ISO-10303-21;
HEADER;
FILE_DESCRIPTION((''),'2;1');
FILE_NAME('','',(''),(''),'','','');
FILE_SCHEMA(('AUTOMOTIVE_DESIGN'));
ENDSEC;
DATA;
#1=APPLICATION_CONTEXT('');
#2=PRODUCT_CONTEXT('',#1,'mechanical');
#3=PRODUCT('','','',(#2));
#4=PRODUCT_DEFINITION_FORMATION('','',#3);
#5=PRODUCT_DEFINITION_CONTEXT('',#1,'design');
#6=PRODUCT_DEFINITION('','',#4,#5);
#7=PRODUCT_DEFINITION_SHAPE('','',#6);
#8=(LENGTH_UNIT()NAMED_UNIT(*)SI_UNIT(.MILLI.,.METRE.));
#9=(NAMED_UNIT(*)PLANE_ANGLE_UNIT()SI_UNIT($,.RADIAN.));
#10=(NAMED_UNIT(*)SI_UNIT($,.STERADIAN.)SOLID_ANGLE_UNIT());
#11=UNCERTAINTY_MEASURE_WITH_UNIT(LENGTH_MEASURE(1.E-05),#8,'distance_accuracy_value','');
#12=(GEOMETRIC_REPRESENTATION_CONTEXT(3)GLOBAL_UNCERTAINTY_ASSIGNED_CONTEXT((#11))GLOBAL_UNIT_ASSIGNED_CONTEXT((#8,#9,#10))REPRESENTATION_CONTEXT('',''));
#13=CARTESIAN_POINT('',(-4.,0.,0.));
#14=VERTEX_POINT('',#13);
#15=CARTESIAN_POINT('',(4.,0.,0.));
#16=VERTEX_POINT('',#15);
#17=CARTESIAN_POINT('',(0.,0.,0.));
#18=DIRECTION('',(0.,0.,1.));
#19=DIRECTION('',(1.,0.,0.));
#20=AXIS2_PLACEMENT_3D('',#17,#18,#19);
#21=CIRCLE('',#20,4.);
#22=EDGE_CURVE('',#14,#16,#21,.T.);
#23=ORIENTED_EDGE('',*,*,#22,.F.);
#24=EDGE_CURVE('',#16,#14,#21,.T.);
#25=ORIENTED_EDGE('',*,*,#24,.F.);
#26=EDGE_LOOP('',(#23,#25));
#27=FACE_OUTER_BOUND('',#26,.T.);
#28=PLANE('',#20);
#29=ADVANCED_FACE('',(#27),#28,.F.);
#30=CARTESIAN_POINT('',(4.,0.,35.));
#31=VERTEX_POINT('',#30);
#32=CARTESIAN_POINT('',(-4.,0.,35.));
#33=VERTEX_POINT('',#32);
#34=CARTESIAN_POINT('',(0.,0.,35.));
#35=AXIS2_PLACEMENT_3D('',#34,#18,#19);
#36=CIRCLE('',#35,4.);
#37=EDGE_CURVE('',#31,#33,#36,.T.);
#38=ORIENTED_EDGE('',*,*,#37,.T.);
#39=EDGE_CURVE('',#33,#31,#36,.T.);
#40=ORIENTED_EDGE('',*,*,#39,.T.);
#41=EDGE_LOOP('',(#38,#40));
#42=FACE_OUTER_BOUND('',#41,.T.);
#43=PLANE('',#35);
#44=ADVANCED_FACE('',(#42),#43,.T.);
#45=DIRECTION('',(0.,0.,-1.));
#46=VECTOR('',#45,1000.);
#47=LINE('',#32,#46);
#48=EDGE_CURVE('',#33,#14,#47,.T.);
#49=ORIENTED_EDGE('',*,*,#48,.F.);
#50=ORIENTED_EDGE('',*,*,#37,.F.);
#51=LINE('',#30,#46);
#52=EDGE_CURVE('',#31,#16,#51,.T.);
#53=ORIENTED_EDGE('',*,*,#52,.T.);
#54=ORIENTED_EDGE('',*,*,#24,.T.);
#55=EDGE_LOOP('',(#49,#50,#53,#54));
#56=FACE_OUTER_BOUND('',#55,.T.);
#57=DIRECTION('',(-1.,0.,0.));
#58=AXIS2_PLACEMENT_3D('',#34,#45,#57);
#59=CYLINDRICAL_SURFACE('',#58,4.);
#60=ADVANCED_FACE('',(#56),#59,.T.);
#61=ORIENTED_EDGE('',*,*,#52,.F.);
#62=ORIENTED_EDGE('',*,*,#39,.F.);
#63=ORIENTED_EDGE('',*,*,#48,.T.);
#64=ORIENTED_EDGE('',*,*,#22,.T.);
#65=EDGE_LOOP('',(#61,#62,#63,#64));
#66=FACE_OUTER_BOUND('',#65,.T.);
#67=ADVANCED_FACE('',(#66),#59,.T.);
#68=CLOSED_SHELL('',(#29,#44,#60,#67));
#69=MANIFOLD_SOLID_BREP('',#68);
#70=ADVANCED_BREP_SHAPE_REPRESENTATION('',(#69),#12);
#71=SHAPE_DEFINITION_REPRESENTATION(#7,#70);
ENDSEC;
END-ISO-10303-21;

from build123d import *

# Parameters (mm, degrees)
SKETCH_1_R      = 4
EXTRUDE_1_DEPTH = 35


with BuildPart() as part:
    # 草图1 → 凸台-拉伸1 (new body)
    with BuildSketch(Plane.XY):
        Circle(SKETCH_1_R)
    extrude(amount=EXTRUDE_1_DEPTH)


solid = part.part
